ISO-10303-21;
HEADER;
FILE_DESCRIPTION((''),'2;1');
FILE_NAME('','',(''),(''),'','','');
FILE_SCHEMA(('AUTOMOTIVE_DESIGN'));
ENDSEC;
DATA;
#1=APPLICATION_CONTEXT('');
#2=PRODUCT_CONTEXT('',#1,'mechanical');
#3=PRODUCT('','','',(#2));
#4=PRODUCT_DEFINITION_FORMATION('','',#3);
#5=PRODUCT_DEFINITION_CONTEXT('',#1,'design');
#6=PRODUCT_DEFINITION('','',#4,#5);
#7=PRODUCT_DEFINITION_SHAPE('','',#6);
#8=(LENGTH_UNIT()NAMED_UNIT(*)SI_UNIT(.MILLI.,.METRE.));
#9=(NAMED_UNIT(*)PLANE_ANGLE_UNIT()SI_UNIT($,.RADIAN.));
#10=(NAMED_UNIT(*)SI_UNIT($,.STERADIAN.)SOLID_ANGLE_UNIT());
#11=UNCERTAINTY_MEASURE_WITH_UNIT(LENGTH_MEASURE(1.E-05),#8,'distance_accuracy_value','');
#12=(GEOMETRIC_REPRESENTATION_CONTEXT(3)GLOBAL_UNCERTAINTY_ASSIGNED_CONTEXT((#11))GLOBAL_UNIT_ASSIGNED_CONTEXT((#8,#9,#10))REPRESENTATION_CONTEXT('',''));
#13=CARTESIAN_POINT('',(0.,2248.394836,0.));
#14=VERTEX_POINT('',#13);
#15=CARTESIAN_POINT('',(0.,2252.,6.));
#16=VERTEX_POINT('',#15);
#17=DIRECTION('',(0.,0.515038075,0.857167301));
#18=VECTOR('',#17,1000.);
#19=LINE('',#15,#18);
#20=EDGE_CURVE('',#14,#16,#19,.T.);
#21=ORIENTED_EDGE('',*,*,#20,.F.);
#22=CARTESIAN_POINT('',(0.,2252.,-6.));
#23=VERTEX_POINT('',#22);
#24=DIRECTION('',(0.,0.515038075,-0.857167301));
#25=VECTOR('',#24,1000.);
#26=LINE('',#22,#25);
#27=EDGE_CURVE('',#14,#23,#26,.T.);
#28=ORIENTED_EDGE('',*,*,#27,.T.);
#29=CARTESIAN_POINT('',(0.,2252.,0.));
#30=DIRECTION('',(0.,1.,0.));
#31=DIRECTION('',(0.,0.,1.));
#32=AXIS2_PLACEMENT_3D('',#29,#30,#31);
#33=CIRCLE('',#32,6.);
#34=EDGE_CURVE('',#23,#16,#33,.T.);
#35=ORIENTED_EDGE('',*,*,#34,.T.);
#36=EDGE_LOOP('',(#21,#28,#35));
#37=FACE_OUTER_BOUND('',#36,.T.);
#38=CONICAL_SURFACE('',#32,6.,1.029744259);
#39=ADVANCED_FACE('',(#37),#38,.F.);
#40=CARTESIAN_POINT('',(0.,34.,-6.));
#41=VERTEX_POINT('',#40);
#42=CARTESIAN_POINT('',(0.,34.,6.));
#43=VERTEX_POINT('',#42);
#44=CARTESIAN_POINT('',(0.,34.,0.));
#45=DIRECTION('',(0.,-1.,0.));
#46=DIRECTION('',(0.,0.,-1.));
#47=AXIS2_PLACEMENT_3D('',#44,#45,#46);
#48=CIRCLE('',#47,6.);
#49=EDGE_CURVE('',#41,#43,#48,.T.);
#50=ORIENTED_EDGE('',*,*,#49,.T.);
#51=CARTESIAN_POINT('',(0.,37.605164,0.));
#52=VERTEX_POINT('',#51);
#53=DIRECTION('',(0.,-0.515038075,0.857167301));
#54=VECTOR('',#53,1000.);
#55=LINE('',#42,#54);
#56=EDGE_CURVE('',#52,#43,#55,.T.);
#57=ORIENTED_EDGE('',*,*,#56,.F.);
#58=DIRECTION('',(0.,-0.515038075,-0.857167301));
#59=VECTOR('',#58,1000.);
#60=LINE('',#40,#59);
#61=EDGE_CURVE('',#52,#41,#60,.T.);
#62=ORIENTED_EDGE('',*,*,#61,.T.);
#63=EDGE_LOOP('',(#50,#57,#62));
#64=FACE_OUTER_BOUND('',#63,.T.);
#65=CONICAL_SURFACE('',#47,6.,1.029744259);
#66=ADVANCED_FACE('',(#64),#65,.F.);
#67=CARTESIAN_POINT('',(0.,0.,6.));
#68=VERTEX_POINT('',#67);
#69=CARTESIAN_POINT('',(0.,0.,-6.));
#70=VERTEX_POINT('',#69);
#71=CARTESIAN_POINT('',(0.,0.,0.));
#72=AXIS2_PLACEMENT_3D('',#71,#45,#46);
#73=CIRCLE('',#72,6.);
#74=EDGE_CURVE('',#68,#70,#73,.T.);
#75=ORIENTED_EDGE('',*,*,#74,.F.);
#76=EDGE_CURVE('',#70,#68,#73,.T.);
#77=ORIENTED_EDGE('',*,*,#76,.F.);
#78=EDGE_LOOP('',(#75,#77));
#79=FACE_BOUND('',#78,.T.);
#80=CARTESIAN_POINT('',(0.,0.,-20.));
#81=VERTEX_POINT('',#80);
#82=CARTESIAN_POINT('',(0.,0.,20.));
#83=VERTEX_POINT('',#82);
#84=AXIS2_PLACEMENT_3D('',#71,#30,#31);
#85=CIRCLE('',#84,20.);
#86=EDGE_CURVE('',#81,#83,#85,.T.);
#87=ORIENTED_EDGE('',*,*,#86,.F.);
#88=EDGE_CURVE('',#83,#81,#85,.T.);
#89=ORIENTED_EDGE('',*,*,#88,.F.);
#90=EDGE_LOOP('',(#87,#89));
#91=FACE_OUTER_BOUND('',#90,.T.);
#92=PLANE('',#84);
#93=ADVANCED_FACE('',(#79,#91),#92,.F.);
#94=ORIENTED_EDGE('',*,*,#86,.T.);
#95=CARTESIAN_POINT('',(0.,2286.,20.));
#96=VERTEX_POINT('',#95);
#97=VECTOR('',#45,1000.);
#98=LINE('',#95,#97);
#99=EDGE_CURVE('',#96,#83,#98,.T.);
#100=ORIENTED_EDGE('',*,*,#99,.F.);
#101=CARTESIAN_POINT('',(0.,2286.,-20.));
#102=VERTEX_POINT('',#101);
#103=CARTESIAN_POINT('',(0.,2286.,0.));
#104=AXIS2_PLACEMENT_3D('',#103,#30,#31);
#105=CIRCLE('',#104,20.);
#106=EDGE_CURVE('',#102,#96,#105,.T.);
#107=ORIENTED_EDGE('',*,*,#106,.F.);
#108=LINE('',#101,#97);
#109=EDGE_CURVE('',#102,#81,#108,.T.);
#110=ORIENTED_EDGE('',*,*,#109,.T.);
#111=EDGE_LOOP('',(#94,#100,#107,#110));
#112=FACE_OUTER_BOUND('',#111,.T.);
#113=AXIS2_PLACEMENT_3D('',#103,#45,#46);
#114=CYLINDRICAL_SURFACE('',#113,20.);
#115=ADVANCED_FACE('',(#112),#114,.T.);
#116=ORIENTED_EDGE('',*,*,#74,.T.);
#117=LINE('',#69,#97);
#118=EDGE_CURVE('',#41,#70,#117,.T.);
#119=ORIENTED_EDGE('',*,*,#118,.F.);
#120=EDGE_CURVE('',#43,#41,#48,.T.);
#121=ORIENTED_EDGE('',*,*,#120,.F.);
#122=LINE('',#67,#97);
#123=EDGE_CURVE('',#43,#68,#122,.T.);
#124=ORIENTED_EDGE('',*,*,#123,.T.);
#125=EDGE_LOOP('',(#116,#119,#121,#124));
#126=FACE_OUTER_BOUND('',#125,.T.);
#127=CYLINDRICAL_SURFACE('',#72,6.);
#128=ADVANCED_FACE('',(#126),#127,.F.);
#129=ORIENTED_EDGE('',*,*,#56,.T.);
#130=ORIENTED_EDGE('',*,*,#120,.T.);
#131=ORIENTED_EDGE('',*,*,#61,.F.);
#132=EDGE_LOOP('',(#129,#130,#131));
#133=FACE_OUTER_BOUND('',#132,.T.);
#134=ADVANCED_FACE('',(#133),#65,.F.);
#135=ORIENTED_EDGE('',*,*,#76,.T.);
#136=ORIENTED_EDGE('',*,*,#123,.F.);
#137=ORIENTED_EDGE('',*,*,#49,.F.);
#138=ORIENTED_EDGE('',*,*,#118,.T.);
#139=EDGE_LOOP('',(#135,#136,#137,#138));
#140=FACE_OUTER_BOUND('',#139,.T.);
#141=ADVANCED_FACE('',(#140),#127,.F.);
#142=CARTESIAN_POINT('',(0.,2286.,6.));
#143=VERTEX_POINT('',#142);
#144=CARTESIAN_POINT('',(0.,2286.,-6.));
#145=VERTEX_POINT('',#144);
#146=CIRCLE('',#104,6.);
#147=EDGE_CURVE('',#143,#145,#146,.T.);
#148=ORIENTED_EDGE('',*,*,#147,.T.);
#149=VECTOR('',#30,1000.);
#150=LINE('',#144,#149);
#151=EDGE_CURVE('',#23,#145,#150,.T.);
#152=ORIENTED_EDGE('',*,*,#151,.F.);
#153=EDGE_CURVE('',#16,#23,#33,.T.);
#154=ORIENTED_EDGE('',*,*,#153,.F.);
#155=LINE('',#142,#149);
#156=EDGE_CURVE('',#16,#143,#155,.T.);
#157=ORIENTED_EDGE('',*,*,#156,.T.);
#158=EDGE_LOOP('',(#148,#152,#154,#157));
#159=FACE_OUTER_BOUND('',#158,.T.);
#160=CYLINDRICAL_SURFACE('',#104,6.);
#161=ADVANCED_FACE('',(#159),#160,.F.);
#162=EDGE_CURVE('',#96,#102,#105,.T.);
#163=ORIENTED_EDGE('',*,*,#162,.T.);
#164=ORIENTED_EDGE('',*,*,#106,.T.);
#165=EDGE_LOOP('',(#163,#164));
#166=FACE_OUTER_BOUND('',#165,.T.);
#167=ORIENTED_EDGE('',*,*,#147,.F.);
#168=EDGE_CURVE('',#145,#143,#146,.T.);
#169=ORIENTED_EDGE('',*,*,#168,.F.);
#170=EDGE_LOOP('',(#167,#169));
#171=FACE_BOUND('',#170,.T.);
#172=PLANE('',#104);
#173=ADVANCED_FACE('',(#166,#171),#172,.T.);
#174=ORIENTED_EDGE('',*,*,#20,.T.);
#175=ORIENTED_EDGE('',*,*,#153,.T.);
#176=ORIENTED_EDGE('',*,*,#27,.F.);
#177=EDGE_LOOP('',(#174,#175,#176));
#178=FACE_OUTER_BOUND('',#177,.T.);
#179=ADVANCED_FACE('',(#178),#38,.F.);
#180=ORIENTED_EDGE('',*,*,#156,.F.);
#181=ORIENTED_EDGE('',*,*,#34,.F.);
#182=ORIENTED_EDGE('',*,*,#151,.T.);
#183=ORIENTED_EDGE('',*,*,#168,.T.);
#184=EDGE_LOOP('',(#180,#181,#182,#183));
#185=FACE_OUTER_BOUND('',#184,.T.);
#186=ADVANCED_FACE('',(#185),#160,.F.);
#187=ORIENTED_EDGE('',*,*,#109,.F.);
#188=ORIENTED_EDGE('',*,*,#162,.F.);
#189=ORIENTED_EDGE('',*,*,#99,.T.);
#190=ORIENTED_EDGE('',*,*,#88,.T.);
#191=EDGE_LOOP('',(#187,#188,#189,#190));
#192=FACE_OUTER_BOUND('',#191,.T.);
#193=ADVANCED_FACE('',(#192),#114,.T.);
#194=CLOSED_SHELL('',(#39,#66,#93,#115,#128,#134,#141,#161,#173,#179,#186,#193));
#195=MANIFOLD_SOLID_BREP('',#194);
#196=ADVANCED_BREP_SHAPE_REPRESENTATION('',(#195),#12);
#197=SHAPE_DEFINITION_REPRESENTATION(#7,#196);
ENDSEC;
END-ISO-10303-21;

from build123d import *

# Parameters (mm, degrees)
SKETCH_1_R              = 20
EXTRUDE_1_DEPTH         = 2286
HOLE_WIZARD_M14_1_D     = 12
HOLE_WIZARD_M14_1_DEPTH = 34
HOLE_WIZARD_M14_1_TIP   = 3.605163714
HOLE_WIZARD_M14_2_D     = 12
HOLE_WIZARD_M14_2_DEPTH = 34
HOLE_WIZARD_M14_2_TIP   = 3.605163714


with BuildPart() as part:
    # 草图1 → 凸台-拉伸1 (new body)
    with BuildSketch(Plane(origin=(0, 0, 0), x_dir=(1, 0, 0), z_dir=(0, 1, 0))):
        with Locations(Location((0, 0, 0), (0, 0, 270))):
            Circle(SKETCH_1_R)
    extrude(amount=EXTRUDE_1_DEPTH)

    # M14 螺纹孔1
    with Locations(Plane(origin=(0, 2286, 0), x_dir=(1, 0, 0), z_dir=(0, 1, 0))):
        with Locations((0, 0)):
            Hole(HOLE_WIZARD_M14_1_D / 2, depth=HOLE_WIZARD_M14_1_DEPTH)
            with Locations((0, 0, -(HOLE_WIZARD_M14_1_DEPTH + HOLE_WIZARD_M14_1_TIP / 2))):  # 118° drill point
                Cone(0, HOLE_WIZARD_M14_1_D / 2, HOLE_WIZARD_M14_1_TIP, mode=Mode.SUBTRACT)

    # M14 螺纹孔2
    with Locations(Plane(origin=(0, 0, 0), x_dir=(-1, 0, 0), z_dir=(0, -1, 0))):
        with Locations((0, 0)):
            Hole(HOLE_WIZARD_M14_2_D / 2, depth=HOLE_WIZARD_M14_2_DEPTH)
            with Locations((0, 0, -(HOLE_WIZARD_M14_2_DEPTH + HOLE_WIZARD_M14_2_TIP / 2))):  # 118° drill point
                Cone(0, HOLE_WIZARD_M14_2_D / 2, HOLE_WIZARD_M14_2_TIP, mode=Mode.SUBTRACT)


solid = part.part
